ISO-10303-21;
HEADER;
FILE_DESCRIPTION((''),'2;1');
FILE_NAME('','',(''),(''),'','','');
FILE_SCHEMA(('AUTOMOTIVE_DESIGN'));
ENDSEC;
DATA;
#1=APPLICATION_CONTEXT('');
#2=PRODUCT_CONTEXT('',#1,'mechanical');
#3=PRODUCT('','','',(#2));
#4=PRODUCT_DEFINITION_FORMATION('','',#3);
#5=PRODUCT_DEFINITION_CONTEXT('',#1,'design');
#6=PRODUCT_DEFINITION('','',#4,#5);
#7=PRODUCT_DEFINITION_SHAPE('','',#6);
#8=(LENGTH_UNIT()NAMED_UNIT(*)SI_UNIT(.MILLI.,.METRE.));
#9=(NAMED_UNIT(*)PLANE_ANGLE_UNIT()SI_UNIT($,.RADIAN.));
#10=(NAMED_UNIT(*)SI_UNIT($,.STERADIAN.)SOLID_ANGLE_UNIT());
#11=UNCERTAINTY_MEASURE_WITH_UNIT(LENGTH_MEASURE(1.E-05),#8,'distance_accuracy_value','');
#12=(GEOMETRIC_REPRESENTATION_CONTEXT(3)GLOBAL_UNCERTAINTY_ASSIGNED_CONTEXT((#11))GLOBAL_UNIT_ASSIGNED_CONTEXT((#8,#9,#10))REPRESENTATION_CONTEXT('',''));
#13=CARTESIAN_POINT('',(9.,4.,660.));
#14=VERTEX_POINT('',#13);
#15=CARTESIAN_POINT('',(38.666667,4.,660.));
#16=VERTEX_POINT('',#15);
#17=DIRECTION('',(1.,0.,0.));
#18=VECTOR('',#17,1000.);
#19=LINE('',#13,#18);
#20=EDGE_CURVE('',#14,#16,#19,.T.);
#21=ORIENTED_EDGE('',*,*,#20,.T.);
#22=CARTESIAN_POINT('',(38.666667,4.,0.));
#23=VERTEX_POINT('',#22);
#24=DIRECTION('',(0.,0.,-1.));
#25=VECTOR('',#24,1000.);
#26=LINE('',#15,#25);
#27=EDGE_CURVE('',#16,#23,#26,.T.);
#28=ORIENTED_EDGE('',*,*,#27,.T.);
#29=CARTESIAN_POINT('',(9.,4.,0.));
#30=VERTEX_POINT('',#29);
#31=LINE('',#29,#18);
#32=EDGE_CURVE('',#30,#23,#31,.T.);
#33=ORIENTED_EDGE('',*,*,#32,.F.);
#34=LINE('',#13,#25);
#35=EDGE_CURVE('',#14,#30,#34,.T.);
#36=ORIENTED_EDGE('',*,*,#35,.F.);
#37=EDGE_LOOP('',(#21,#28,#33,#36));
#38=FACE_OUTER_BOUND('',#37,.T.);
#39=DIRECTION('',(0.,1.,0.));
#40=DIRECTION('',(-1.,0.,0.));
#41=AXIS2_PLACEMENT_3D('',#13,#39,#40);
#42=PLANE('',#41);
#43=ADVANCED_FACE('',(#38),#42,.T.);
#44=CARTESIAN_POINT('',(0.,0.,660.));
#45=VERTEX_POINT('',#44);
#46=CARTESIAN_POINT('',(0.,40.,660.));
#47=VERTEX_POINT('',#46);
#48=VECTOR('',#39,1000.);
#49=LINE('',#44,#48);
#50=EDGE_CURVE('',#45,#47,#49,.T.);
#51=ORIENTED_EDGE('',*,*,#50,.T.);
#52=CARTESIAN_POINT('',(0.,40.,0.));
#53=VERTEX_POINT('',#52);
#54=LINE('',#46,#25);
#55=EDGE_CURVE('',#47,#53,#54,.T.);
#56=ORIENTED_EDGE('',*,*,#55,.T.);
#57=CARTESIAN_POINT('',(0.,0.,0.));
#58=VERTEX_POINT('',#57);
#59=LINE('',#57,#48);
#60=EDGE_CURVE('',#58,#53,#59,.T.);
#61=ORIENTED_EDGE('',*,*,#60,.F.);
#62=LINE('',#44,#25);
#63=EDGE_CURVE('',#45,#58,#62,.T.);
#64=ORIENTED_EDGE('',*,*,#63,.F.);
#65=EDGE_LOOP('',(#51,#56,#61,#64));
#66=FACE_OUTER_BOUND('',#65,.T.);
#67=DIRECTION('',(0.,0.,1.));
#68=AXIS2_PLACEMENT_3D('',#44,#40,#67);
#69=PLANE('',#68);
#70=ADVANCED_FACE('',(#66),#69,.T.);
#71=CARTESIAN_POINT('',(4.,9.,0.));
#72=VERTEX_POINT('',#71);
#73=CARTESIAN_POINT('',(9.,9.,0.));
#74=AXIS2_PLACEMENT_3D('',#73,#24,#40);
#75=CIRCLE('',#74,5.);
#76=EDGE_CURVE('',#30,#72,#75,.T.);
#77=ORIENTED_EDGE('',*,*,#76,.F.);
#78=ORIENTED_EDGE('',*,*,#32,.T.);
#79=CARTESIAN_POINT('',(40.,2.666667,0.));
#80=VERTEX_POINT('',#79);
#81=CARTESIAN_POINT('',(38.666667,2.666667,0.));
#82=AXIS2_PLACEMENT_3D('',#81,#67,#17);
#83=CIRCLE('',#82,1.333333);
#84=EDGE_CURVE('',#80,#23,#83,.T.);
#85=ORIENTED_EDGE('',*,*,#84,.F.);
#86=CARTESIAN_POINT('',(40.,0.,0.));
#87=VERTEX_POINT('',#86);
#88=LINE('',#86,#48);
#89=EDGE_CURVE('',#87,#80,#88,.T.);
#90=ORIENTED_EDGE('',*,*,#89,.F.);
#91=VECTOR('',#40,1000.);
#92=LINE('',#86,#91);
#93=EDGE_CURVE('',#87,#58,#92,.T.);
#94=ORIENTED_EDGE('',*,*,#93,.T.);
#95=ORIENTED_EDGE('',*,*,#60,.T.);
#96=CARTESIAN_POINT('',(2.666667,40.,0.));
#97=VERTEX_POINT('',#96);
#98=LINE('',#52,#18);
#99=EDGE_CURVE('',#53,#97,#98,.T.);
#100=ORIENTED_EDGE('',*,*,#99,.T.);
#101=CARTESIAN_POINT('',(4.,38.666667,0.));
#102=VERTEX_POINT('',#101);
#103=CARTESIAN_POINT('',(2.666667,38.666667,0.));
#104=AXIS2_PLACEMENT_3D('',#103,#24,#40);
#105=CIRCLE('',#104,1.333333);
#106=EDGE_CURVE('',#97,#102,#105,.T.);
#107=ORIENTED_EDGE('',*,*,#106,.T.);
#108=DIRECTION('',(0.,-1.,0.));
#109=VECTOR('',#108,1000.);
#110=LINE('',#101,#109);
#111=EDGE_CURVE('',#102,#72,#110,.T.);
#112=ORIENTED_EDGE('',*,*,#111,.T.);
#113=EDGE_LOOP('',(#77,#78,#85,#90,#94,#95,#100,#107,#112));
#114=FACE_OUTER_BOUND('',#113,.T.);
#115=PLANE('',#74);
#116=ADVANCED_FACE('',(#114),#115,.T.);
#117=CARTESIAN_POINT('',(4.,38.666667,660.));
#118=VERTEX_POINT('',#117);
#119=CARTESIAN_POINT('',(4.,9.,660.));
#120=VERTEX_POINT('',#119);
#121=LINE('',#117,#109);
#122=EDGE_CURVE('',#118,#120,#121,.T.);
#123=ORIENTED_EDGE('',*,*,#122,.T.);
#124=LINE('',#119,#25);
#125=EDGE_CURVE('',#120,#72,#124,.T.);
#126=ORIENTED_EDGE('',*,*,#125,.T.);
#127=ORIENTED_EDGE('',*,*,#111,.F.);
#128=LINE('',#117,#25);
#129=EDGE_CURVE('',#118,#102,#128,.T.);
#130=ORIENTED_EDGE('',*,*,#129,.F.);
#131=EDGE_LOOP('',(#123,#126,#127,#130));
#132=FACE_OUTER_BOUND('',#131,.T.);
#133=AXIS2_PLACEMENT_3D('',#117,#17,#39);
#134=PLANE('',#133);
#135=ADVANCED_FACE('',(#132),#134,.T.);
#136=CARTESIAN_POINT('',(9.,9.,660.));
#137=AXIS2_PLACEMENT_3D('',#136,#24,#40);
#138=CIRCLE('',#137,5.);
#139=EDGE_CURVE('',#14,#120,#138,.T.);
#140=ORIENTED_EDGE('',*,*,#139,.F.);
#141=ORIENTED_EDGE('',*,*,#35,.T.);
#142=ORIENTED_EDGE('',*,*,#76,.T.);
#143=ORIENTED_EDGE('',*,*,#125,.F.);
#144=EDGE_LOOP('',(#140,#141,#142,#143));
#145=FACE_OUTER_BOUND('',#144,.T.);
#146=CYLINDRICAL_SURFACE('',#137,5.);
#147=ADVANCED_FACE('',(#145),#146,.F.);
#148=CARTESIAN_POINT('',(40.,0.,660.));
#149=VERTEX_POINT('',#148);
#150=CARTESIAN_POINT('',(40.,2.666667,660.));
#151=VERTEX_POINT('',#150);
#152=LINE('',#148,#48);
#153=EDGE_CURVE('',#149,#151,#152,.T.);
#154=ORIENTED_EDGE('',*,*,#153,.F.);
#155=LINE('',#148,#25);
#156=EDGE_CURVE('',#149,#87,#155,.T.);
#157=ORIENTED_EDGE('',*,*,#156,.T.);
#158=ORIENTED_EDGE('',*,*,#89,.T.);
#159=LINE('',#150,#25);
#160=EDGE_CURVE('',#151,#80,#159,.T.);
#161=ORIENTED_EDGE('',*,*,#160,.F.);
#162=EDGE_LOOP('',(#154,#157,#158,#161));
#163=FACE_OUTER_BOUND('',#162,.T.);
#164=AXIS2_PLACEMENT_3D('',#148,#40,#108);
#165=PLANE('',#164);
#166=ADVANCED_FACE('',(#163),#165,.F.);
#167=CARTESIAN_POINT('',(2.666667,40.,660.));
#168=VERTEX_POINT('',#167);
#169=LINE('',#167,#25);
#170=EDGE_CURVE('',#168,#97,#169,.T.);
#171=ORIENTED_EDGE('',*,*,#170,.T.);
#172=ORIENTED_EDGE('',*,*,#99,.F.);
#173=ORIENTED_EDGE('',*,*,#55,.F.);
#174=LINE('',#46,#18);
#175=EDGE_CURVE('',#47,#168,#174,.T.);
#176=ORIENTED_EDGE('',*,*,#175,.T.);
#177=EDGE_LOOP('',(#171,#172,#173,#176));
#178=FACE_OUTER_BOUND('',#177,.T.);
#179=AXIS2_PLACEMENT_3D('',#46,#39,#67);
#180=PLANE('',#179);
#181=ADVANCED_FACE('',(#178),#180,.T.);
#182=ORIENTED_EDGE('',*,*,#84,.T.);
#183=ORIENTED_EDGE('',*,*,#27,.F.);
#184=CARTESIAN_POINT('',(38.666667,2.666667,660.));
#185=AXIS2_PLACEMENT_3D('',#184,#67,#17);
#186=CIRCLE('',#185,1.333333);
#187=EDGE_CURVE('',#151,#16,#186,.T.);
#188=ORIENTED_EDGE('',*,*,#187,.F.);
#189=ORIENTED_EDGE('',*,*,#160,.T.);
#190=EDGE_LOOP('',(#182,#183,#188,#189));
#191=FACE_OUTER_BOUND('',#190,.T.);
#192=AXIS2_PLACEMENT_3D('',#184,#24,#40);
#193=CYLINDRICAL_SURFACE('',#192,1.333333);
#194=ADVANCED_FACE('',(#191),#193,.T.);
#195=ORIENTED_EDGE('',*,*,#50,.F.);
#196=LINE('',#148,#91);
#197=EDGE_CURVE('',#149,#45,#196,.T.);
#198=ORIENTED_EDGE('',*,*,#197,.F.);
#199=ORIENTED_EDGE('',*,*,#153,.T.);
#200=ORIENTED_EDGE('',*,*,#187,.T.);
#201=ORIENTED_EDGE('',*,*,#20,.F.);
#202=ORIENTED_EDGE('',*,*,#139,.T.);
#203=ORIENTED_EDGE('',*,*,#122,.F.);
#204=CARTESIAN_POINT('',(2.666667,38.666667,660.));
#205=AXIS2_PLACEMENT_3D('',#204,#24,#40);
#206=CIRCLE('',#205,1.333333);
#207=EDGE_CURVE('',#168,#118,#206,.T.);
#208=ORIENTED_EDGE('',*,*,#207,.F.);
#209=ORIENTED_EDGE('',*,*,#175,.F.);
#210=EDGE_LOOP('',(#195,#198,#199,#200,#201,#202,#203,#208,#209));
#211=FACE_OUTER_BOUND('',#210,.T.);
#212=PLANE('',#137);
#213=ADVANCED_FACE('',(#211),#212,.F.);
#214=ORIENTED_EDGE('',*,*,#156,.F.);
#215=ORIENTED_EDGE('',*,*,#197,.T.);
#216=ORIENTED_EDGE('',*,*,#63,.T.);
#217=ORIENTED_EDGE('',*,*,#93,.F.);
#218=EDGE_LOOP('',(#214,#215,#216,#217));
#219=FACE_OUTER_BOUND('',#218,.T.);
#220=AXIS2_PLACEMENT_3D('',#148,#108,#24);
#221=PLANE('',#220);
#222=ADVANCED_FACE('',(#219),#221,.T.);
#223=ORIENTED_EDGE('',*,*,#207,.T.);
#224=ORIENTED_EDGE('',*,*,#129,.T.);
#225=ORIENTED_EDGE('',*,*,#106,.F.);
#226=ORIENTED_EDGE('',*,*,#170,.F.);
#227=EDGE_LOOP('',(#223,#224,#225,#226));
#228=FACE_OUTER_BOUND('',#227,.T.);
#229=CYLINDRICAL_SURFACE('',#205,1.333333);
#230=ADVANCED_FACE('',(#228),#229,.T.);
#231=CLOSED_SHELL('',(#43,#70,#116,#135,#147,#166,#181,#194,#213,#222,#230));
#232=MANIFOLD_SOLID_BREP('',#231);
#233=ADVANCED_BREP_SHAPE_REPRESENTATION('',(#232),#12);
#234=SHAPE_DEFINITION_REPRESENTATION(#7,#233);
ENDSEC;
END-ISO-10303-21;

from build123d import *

# Parameters (mm, degrees)
BOSS_EXTRUDE1_DEPTH = 660


with BuildPart() as part:
    # Sketch1 → Boss-Extrude1 (new body)
    with BuildSketch(Plane.XY):
        with BuildLine():
            Line((0, 0), (0, 40))
            Line((0, 40), (2.666666667, 40))
            ThreePointArc((2.666666667, 40), (3.609475708, 39.609475708), (4, 38.666666667))
            Line((4, 38.666666667), (4, 9))
            ThreePointArc((4, 9), (5.464466094, 5.464466094), (9, 4))
            Line((9, 4), (38.666666667, 4))
            ThreePointArc((38.666666667, 4), (39.609475708, 3.609475708), (40, 2.666666667))
            Line((40, 2.666666667), (40, 0))
            Line((40, 0), (0, 0))
        make_face()
    extrude(amount=BOSS_EXTRUDE1_DEPTH)


solid = part.part
